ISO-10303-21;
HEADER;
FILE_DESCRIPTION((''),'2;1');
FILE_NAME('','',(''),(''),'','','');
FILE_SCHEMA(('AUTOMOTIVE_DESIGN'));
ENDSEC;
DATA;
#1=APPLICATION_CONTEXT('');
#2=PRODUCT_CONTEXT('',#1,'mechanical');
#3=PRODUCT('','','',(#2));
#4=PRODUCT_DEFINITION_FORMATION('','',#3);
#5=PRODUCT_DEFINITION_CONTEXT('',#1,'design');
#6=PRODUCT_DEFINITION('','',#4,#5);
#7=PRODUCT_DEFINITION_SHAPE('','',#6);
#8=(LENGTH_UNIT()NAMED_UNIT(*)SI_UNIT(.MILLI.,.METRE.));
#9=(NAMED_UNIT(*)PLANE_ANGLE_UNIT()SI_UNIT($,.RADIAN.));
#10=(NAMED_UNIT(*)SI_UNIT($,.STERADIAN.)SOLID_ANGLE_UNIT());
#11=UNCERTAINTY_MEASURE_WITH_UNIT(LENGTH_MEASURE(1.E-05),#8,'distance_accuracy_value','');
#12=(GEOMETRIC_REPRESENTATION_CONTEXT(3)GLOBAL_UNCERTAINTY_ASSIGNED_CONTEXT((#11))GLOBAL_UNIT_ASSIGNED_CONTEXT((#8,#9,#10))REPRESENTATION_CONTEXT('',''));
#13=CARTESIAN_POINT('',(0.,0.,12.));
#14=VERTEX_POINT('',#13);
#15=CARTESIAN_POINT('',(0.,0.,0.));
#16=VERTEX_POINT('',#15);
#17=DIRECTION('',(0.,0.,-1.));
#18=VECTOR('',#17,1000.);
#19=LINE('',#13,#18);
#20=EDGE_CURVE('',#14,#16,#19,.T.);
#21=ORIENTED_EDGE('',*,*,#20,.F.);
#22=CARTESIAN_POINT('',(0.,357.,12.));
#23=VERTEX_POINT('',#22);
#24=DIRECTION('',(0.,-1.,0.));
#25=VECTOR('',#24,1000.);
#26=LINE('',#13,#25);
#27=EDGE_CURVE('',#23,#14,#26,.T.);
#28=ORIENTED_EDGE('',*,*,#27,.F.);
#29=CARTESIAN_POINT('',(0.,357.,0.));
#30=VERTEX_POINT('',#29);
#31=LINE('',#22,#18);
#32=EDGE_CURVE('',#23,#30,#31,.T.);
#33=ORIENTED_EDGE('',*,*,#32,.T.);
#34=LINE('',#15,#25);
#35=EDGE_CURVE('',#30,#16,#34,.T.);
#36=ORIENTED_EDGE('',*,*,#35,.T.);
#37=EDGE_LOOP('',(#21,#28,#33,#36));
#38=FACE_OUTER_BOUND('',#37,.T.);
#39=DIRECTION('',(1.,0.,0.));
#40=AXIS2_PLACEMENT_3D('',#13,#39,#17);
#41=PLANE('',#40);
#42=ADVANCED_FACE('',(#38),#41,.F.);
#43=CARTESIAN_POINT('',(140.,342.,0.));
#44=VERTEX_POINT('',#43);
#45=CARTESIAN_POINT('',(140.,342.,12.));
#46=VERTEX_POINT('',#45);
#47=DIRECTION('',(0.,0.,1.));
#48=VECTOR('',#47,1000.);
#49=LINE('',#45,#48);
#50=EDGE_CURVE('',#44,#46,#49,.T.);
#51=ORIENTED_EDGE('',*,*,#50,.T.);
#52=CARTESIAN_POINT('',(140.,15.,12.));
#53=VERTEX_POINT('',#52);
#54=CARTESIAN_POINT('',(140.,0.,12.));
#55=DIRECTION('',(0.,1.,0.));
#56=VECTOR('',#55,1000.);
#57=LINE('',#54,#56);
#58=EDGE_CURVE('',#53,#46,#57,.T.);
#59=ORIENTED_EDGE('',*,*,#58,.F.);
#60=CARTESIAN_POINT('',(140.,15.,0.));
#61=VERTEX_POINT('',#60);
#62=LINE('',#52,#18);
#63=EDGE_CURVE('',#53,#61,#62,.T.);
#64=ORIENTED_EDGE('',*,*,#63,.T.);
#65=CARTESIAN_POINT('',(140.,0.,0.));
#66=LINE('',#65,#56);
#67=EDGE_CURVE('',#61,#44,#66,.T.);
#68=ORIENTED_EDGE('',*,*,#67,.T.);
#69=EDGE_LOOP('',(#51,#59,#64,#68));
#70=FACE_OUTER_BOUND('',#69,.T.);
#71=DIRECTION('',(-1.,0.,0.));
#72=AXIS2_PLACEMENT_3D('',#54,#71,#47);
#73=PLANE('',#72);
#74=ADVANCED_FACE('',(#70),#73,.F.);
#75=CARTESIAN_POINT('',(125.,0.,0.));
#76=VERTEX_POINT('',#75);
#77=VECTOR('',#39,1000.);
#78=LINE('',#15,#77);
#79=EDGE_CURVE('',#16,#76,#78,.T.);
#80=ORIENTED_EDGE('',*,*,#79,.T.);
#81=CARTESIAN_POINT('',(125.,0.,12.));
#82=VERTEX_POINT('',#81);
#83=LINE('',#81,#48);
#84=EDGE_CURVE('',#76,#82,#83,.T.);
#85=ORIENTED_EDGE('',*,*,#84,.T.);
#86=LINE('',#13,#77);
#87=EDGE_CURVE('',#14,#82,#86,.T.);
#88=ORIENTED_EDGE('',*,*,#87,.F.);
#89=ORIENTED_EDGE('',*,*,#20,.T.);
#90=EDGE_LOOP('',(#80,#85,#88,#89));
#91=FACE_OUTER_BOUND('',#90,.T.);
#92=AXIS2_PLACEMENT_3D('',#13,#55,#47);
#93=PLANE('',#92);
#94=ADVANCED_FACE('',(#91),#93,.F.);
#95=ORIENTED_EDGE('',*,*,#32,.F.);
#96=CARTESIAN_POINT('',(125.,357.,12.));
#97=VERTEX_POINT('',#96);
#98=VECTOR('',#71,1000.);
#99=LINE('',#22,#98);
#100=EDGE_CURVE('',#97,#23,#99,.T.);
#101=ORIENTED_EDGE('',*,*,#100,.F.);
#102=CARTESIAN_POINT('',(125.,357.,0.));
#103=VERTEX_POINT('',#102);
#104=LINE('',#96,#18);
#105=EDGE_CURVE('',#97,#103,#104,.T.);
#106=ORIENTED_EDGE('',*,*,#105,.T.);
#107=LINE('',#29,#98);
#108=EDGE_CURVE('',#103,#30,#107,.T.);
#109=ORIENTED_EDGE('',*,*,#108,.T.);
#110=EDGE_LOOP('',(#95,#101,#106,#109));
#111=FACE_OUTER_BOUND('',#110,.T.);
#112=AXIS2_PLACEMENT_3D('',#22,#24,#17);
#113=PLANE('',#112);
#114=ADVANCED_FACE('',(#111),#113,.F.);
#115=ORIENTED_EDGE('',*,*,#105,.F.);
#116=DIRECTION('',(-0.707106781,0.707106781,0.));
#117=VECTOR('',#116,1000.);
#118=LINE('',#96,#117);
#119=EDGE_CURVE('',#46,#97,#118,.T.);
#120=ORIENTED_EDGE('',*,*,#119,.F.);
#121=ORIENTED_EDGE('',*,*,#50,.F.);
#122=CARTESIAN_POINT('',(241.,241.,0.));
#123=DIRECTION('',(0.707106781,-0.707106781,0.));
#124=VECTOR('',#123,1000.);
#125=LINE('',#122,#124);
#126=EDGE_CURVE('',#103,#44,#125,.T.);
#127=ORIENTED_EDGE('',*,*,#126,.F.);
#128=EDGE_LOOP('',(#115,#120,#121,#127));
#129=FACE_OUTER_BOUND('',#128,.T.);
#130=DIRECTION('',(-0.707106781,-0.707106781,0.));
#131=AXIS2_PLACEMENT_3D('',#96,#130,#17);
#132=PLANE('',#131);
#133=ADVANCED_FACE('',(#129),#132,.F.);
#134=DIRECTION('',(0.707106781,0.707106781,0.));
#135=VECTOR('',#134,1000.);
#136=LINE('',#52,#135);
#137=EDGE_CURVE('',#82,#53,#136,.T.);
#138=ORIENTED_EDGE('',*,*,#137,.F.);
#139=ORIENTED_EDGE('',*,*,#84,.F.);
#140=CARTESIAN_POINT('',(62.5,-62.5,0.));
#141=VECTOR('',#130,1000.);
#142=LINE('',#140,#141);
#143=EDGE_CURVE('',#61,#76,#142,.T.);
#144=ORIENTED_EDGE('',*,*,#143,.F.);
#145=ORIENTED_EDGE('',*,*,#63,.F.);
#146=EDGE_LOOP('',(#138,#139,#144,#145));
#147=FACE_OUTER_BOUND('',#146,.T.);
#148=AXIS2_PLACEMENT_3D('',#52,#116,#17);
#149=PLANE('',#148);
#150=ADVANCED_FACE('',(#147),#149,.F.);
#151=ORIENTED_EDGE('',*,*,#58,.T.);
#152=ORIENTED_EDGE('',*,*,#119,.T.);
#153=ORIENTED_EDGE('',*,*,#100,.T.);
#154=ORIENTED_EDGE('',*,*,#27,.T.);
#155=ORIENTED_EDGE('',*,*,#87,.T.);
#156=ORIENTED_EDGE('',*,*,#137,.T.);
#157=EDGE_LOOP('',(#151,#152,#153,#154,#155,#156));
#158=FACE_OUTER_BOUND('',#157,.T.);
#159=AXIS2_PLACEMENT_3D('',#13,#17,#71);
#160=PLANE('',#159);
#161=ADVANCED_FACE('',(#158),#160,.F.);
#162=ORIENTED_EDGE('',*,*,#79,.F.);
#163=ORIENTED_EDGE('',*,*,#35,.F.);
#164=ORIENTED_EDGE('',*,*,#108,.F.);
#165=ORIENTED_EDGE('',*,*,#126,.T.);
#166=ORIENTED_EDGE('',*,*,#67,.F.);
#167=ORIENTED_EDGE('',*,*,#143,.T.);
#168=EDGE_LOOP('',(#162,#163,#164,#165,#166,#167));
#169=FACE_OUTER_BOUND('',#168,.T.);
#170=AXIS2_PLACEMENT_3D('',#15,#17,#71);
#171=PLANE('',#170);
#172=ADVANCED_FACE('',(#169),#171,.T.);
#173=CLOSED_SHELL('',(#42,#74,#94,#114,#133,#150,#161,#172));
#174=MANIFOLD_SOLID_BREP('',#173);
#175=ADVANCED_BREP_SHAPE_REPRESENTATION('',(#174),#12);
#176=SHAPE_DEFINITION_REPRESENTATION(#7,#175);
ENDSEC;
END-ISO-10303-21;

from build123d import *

# Parameters (mm, degrees)
SKETCH1_W           = 140
SKETCH1_H           = 357
BOSS_EXTRUDE1_DEPTH = 12
CHAMFER2_SIZE       = 15


with BuildPart() as part:
    # Sketch1 → Boss-Extrude1 (new body)
    with BuildSketch(Plane.XY):
        with Locations((70, 178.5)):
            Rectangle(SKETCH1_W, SKETCH1_H)
    extrude(amount=BOSS_EXTRUDE1_DEPTH)

    # Chamfer2
    chamfer2_edges = [part.edges().sort_by_distance(p)[0] for p in [
        (140, 357, 6),
        (140, 0, 6),
    ]]
    chamfer(chamfer2_edges, length=CHAMFER2_SIZE)


solid = part.part
